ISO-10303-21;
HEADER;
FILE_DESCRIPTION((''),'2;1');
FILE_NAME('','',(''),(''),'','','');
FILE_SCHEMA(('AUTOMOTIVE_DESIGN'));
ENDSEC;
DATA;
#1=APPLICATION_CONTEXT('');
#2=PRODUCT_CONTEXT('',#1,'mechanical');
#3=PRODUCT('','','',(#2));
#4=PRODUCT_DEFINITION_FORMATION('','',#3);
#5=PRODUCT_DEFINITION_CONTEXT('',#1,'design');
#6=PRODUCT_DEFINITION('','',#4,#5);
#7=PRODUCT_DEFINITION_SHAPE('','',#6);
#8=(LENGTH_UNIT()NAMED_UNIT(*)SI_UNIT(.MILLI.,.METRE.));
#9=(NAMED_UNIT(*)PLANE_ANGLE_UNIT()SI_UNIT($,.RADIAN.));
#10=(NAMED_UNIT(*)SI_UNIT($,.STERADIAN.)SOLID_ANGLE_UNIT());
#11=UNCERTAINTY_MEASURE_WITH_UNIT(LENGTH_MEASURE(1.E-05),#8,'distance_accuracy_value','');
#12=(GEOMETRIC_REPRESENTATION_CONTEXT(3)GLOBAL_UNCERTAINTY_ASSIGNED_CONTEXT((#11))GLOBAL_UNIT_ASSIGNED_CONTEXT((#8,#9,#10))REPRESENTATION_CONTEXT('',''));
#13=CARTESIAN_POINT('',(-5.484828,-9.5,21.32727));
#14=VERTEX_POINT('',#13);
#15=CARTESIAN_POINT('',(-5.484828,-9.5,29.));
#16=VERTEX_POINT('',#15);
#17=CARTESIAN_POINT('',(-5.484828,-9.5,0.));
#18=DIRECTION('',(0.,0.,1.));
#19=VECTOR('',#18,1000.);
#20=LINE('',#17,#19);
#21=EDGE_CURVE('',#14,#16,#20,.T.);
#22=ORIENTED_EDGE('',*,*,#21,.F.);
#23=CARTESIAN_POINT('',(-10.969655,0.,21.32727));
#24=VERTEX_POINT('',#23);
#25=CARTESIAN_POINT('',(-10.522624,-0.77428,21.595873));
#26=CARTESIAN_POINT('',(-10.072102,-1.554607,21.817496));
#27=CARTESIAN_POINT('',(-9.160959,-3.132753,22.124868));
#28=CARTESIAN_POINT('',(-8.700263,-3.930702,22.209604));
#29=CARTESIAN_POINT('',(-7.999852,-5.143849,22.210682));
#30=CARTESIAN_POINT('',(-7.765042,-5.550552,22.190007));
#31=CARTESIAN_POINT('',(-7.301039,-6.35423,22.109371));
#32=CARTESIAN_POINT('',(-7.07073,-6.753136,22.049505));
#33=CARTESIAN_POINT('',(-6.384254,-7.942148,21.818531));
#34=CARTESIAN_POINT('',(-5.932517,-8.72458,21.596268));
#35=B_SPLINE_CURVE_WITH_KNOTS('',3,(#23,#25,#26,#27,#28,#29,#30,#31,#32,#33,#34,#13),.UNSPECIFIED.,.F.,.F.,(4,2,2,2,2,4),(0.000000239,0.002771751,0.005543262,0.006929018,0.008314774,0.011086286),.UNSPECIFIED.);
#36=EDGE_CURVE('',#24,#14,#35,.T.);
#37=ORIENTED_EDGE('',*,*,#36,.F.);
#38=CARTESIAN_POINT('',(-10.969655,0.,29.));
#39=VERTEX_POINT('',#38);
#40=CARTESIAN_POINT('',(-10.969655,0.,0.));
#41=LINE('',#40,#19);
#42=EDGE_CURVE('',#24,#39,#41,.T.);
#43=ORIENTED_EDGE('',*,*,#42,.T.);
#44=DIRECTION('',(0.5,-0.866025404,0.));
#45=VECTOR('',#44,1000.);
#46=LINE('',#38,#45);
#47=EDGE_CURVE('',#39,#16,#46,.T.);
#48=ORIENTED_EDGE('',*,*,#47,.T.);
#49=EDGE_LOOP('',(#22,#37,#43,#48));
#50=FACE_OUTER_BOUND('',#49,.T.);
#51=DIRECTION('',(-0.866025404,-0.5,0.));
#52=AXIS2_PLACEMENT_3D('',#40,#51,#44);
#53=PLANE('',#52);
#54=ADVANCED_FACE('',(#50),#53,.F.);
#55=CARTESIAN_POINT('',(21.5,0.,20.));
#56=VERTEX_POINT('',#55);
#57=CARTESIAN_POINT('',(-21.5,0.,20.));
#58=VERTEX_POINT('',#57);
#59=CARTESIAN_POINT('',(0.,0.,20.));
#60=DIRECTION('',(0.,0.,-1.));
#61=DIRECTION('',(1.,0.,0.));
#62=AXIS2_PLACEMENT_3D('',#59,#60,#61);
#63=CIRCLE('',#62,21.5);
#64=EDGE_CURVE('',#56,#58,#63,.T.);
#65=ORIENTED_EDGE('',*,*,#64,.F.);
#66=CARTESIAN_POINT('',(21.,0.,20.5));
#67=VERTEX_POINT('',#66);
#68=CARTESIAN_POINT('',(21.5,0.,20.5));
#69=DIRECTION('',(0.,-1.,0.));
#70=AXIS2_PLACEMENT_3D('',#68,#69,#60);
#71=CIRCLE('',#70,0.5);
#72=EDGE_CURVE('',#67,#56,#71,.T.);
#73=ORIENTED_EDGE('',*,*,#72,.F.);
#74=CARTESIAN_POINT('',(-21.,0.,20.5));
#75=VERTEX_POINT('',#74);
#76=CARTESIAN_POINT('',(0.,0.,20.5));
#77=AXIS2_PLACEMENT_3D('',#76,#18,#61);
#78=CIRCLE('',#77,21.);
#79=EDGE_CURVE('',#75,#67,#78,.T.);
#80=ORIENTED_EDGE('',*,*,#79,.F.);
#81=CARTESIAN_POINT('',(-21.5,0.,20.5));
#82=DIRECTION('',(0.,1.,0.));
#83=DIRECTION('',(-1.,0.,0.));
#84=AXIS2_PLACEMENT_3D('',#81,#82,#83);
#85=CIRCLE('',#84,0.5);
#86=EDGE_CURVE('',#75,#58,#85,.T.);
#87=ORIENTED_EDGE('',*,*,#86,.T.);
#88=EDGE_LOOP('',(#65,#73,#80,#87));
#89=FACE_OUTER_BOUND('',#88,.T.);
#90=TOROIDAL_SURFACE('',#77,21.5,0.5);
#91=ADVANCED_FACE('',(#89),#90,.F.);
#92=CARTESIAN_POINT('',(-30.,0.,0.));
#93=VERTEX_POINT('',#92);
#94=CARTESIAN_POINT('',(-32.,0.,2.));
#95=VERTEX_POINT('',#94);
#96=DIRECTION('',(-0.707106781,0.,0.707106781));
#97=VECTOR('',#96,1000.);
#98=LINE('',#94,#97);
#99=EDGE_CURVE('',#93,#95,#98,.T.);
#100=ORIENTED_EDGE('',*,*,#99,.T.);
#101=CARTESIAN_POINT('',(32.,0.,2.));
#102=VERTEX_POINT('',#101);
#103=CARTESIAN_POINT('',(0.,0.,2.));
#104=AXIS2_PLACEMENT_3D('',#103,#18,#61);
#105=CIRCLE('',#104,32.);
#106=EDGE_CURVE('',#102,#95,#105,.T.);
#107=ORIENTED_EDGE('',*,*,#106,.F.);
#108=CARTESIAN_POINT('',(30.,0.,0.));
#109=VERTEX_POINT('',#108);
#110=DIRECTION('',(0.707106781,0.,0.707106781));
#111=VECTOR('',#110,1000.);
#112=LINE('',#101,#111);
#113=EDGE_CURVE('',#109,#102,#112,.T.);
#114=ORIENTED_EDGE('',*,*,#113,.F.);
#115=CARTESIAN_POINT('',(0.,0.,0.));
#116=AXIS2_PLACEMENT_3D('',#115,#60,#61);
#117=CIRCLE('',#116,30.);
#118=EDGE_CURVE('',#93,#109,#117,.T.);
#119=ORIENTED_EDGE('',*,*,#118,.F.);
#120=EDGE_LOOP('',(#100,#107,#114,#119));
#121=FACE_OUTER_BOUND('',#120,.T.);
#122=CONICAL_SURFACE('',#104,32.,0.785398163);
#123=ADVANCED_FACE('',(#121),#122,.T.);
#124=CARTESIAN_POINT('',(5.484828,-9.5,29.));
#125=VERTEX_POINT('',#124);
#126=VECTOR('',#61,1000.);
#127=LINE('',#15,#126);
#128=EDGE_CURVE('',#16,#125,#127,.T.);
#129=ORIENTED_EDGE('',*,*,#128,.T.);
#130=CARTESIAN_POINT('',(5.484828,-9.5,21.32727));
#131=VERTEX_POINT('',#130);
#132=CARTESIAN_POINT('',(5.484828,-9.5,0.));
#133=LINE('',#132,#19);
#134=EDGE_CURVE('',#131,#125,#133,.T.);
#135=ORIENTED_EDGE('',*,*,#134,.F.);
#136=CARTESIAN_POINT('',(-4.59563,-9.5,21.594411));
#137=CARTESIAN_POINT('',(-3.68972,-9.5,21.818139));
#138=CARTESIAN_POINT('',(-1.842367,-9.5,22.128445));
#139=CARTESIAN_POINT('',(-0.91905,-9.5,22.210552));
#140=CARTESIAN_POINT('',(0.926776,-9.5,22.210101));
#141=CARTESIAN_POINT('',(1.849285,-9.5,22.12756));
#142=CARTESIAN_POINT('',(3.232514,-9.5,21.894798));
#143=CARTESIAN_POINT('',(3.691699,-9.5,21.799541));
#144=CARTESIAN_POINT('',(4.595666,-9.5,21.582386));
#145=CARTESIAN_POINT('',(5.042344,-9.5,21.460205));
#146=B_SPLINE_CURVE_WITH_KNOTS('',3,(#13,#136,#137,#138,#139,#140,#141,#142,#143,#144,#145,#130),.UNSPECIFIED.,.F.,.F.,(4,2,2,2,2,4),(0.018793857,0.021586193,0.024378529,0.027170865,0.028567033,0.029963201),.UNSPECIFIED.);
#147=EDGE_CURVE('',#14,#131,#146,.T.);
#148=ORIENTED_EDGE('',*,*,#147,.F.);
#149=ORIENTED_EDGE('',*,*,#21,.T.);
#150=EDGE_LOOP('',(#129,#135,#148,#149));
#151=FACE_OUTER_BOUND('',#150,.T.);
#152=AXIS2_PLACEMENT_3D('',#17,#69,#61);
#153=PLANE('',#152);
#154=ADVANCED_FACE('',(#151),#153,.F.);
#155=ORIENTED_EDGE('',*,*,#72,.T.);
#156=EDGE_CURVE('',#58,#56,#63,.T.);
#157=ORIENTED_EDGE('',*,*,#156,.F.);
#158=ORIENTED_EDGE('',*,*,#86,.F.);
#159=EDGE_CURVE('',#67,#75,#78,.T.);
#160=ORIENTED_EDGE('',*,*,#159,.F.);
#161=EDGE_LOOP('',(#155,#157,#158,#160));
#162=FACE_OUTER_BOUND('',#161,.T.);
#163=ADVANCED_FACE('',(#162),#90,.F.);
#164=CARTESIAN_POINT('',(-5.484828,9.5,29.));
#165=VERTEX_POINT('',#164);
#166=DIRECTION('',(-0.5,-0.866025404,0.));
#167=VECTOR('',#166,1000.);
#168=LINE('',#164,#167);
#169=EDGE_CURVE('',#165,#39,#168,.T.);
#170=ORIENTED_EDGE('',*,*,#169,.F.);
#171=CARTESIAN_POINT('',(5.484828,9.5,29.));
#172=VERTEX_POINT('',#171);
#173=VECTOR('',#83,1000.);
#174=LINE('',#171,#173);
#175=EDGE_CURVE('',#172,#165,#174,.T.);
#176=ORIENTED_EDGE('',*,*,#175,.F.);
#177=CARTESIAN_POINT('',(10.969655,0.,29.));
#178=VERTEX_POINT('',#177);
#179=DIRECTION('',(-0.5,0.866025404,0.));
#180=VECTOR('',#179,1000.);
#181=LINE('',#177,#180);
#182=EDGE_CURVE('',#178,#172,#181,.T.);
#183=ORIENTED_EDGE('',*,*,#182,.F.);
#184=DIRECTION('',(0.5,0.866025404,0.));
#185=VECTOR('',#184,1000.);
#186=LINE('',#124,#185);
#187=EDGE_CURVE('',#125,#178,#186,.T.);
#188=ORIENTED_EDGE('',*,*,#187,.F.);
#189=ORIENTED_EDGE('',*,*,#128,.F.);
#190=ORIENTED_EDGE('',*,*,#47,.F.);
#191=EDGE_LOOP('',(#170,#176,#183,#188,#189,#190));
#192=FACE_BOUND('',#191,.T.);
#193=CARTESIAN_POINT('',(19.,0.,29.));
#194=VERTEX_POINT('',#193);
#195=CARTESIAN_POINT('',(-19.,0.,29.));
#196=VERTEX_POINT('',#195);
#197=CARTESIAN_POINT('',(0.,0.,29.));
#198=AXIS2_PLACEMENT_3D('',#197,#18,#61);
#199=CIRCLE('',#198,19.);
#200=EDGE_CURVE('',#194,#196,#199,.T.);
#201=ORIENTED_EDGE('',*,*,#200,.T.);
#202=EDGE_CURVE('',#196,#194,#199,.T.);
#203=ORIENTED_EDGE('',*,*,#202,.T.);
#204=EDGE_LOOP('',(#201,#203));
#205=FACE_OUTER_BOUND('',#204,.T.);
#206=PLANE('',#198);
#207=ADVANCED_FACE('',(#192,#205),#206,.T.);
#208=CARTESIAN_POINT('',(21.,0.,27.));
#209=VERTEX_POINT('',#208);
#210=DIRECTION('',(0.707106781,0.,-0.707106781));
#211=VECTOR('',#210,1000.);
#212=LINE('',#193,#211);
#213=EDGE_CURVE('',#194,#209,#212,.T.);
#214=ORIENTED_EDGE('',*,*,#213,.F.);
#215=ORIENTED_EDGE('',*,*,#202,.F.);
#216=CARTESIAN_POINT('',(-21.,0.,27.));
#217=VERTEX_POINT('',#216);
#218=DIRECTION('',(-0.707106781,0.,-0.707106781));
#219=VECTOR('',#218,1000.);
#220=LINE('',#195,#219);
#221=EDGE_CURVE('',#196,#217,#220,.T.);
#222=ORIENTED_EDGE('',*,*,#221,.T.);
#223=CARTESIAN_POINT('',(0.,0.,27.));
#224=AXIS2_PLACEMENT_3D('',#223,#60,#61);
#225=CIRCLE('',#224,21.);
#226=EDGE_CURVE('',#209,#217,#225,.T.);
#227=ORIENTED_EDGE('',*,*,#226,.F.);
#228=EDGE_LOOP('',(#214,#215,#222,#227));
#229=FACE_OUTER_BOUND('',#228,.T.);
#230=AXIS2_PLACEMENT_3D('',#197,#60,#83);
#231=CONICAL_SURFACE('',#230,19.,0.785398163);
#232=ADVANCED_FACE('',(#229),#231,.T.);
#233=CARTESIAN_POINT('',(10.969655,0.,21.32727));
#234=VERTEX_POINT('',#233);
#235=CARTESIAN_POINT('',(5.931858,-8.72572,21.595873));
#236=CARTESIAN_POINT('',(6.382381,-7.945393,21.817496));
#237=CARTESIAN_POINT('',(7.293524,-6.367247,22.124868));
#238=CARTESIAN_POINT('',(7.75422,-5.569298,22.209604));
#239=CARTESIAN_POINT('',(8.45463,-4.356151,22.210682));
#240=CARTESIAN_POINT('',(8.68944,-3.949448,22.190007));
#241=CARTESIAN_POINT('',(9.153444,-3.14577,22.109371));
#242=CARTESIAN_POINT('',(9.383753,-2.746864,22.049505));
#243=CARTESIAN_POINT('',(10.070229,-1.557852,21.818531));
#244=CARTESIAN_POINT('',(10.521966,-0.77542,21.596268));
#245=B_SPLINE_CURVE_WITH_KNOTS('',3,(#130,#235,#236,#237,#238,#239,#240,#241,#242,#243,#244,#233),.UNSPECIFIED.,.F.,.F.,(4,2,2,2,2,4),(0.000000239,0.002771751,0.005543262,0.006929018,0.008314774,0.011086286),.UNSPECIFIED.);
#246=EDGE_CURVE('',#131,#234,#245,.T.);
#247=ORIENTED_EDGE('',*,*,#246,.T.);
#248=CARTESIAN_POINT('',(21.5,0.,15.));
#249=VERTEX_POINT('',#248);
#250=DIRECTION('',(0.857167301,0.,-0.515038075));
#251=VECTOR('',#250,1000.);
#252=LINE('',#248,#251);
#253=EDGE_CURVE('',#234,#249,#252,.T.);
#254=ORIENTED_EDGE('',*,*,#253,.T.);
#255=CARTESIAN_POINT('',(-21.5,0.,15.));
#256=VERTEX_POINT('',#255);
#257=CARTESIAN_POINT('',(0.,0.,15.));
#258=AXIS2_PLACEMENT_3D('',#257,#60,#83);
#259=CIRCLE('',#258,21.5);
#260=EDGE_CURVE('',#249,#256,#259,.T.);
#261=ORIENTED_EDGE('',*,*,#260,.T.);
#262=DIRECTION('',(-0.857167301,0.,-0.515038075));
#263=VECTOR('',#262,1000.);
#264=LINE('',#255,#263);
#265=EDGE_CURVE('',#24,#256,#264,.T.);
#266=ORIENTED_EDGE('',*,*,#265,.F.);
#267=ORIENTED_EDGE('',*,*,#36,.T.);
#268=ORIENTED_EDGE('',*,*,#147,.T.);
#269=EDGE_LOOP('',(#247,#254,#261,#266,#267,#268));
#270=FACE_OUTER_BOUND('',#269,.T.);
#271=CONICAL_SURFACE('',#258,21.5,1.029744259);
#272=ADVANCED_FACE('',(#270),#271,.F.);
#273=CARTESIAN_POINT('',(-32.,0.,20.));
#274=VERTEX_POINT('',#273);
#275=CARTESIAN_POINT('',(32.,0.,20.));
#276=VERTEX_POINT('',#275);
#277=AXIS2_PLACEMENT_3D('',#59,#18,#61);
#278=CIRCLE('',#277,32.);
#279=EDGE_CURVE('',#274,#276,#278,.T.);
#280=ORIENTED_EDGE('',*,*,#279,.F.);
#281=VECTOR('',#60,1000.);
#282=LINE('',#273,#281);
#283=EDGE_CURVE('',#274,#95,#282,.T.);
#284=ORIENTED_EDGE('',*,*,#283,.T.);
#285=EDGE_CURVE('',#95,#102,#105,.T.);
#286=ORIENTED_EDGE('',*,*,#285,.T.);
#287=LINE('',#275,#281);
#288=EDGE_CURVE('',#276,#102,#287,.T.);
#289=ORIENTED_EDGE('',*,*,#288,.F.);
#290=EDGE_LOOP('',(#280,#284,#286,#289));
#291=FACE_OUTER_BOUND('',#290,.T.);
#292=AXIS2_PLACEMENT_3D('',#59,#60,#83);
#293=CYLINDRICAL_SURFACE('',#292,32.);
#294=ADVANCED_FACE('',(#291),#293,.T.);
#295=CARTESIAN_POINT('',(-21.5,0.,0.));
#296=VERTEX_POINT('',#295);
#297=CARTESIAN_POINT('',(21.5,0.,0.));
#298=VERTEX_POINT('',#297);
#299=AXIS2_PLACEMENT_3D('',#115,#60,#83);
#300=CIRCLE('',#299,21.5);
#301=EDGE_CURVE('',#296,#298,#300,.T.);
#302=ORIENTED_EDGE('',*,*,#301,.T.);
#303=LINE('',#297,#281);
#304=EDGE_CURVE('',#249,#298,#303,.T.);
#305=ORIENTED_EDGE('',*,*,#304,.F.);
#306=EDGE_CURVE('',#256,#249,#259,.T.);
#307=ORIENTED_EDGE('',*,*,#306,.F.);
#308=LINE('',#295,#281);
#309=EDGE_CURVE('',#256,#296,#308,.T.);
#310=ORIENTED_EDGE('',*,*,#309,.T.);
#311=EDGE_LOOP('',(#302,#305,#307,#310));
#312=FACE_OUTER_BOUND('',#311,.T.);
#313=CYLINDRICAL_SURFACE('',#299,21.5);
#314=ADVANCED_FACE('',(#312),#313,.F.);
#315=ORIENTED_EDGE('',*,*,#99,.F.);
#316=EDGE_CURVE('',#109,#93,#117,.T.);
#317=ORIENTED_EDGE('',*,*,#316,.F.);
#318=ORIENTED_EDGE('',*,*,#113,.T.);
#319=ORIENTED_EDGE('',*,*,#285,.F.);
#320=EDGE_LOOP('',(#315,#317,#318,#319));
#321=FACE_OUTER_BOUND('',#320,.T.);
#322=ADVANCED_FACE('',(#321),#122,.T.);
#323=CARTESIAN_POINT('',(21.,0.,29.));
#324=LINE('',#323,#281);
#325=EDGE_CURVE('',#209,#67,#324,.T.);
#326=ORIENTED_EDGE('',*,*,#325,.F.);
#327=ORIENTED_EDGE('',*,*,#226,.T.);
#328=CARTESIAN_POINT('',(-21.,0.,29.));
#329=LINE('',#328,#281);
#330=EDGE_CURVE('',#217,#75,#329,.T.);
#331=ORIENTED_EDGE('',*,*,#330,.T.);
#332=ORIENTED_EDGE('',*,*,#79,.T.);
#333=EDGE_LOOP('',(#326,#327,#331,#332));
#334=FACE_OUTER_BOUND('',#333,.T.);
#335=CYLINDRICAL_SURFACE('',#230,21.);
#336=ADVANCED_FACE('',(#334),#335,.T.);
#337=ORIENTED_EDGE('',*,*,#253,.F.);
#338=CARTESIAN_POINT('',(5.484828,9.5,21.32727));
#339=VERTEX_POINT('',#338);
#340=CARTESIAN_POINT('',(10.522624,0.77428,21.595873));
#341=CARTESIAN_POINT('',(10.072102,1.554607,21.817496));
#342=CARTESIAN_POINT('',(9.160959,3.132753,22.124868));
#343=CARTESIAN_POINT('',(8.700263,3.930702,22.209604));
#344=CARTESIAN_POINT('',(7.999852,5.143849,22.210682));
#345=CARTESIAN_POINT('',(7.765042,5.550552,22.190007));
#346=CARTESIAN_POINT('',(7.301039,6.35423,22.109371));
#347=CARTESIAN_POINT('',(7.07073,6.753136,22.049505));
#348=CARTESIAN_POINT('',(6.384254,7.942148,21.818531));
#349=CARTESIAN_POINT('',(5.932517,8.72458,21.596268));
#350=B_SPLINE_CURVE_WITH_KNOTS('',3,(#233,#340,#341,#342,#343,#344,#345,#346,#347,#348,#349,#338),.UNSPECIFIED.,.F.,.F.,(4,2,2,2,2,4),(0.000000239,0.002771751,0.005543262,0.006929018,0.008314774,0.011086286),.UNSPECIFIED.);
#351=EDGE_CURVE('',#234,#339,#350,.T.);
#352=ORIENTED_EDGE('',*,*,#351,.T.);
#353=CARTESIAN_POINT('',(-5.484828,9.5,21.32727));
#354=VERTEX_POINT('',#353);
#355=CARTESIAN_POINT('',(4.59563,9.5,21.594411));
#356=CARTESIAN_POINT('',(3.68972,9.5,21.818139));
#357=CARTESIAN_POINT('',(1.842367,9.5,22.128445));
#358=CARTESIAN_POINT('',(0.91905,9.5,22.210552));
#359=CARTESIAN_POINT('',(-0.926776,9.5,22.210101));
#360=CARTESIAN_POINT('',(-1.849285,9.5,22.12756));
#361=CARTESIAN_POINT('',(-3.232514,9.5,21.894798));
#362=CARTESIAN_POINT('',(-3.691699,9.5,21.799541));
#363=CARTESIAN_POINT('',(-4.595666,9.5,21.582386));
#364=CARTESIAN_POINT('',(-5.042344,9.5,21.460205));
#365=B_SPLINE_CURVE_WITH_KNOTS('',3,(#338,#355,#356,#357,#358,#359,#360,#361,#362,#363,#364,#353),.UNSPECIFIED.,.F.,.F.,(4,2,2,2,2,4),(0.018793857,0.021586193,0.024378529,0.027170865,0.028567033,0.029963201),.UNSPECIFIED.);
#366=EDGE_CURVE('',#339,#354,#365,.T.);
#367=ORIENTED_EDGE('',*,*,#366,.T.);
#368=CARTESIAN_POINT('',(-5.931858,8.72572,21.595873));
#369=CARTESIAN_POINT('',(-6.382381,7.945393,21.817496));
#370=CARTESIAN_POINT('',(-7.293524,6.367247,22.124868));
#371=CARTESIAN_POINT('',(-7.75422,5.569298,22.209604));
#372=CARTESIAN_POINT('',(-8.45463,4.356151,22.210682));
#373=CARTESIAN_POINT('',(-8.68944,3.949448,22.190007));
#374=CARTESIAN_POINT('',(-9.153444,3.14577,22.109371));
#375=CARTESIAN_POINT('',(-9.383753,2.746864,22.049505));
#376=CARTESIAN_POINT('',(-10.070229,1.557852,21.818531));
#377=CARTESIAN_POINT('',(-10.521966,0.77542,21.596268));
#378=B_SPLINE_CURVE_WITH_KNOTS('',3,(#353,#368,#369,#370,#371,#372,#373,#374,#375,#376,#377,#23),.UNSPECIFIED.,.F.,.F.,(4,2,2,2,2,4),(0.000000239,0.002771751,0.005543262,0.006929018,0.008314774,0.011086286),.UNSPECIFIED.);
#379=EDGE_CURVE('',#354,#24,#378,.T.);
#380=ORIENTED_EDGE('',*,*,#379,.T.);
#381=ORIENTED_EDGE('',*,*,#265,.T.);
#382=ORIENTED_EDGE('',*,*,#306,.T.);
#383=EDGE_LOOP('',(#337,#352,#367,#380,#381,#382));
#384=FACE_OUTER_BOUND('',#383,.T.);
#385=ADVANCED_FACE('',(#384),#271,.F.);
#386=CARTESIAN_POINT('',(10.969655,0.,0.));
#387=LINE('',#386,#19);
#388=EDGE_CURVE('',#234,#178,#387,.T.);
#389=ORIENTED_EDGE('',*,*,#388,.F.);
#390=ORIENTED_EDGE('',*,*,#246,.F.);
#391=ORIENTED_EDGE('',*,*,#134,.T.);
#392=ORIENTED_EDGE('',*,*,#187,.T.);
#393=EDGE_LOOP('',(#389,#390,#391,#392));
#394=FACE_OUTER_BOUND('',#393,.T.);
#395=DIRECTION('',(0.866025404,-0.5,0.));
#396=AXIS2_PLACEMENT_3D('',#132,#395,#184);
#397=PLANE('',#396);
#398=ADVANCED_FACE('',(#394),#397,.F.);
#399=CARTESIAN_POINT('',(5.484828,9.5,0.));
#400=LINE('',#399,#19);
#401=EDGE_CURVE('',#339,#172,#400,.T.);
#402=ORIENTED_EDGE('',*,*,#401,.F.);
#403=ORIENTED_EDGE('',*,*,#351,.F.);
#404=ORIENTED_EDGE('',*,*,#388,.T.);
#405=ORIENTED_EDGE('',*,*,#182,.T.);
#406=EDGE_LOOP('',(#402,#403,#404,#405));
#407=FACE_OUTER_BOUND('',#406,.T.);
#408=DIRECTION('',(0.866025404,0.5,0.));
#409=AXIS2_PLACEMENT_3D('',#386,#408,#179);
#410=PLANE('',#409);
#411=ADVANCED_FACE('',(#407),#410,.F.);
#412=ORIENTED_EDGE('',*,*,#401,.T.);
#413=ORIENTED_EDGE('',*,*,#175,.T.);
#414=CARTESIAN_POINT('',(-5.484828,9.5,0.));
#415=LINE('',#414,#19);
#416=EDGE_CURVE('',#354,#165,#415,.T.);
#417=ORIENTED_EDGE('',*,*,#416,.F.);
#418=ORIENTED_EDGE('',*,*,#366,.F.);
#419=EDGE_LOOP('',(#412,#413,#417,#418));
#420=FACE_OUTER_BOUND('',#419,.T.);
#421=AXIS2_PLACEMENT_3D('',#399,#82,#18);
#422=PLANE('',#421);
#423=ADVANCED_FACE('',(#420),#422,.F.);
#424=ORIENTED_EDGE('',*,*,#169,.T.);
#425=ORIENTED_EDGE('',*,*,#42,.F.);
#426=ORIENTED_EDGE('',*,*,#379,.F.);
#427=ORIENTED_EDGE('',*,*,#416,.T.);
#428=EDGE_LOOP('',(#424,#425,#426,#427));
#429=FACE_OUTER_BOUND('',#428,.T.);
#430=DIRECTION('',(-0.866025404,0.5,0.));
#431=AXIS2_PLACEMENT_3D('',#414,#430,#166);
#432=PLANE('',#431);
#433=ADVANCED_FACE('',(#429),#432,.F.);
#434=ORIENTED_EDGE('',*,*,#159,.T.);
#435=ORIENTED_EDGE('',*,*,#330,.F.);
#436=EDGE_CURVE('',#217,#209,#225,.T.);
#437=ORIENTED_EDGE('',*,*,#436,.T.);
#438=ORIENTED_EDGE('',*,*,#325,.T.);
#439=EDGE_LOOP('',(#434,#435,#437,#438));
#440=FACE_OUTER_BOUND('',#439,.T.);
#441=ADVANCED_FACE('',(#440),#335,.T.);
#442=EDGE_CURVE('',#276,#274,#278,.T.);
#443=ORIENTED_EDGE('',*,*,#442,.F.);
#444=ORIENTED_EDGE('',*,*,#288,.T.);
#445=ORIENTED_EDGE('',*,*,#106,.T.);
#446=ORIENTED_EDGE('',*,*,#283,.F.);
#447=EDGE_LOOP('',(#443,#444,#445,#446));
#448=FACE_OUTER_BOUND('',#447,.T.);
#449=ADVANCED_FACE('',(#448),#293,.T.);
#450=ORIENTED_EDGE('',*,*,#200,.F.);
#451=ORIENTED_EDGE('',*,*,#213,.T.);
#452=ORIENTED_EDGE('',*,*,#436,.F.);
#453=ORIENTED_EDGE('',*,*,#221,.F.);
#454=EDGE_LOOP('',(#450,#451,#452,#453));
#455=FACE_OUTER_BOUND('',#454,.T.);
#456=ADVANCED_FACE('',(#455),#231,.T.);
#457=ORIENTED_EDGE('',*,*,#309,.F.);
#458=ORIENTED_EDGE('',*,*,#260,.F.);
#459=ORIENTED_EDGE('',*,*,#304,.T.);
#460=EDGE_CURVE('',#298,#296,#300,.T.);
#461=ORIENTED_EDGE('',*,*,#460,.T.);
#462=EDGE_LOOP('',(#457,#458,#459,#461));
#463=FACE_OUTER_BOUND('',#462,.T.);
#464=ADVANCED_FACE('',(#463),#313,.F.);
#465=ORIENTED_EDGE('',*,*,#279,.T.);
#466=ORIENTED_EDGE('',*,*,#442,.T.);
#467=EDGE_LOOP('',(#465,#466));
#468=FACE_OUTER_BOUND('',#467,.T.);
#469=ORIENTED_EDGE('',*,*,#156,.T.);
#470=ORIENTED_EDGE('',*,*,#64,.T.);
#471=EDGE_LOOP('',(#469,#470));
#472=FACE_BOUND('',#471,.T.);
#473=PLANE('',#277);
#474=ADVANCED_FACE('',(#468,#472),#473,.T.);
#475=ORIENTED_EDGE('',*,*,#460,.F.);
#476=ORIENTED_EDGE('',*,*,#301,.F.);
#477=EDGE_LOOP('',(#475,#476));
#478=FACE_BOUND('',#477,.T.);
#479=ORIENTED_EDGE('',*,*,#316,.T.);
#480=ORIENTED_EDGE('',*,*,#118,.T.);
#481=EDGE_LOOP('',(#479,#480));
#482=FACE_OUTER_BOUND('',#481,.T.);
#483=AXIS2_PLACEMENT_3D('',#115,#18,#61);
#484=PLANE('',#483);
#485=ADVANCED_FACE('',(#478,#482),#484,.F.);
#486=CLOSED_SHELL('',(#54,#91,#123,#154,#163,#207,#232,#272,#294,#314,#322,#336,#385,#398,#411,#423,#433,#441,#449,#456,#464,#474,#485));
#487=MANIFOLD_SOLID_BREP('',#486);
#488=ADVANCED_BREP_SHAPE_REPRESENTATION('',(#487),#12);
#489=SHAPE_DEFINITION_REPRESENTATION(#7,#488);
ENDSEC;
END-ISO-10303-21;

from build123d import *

# Parameters (mm, degrees)
SKETCH_1_R              = 32
EXTRUDE_1_DEPTH         = 20
SKETCH_2_R              = 21
EXTRUDE_2_DEPTH         = 9
HOLE_WIZARD_M48_1_D     = 43
HOLE_WIZARD_M48_1_DEPTH = 15
HOLE_WIZARD_M48_1_TIP   = 12.918503309
CUT_EXTRUDE_1_DEPTH     = 54.749418602
CHAMFER_2_SIZE          = 2
CHAMFER_3_SIZE          = 2
FILLET_1_R              = 0.5


with BuildPart() as part:
    # 草图1 → 凸台-拉伸1 (new body)
    with BuildSketch(Plane.XY):
        Circle(SKETCH_1_R)
    extrude(amount=EXTRUDE_1_DEPTH)

    # 草图2 → 凸台-拉伸2 (add)
    with BuildSketch(Plane.XY.offset(20)):
        Circle(SKETCH_2_R)
    extrude(amount=EXTRUDE_2_DEPTH)

    # M48 螺纹孔1
    with Locations(Plane(origin=(0, 0, 0), x_dir=(-1, 0, 0), z_dir=(0, 0, -1))):
        with Locations((0, 0)):
            Hole(HOLE_WIZARD_M48_1_D / 2, depth=HOLE_WIZARD_M48_1_DEPTH)
            with Locations((0, 0, -(HOLE_WIZARD_M48_1_DEPTH + HOLE_WIZARD_M48_1_TIP / 2))):  # 118° drill point
                Cone(0, HOLE_WIZARD_M48_1_D / 2, HOLE_WIZARD_M48_1_TIP, mode=Mode.SUBTRACT)

    # 草图5 → 切除-拉伸1 (cut, through all)
    with BuildSketch(Plane.XY.offset(29)):
        Polygon((10.969655115, 0), (5.484827557, 9.5), (-5.484827557, 9.5), (-10.969655115, 0), (-5.484827557, -9.5), (5.484827557, -9.5), align=None)
    extrude(amount=-CUT_EXTRUDE_1_DEPTH, mode=Mode.SUBTRACT)

    # 倒角2
    chamfer_2_edges = [part.edges().sort_by_distance(p)[0] for p in [
        (-32, 0, 0),
    ]]
    chamfer(chamfer_2_edges, length=CHAMFER_2_SIZE)

    # 倒角3
    chamfer_3_edges = [part.edges().sort_by_distance(p)[0] for p in [
        (-21, 0, 29),
    ]]
    chamfer(chamfer_3_edges, length=CHAMFER_3_SIZE)

    # 圆角1
    fillet_1_edges = [part.edges().sort_by_distance(p)[0] for p in [
        (-21, 0, 20),
    ]]
    fillet(fillet_1_edges, radius=FILLET_1_R)


solid = part.part
